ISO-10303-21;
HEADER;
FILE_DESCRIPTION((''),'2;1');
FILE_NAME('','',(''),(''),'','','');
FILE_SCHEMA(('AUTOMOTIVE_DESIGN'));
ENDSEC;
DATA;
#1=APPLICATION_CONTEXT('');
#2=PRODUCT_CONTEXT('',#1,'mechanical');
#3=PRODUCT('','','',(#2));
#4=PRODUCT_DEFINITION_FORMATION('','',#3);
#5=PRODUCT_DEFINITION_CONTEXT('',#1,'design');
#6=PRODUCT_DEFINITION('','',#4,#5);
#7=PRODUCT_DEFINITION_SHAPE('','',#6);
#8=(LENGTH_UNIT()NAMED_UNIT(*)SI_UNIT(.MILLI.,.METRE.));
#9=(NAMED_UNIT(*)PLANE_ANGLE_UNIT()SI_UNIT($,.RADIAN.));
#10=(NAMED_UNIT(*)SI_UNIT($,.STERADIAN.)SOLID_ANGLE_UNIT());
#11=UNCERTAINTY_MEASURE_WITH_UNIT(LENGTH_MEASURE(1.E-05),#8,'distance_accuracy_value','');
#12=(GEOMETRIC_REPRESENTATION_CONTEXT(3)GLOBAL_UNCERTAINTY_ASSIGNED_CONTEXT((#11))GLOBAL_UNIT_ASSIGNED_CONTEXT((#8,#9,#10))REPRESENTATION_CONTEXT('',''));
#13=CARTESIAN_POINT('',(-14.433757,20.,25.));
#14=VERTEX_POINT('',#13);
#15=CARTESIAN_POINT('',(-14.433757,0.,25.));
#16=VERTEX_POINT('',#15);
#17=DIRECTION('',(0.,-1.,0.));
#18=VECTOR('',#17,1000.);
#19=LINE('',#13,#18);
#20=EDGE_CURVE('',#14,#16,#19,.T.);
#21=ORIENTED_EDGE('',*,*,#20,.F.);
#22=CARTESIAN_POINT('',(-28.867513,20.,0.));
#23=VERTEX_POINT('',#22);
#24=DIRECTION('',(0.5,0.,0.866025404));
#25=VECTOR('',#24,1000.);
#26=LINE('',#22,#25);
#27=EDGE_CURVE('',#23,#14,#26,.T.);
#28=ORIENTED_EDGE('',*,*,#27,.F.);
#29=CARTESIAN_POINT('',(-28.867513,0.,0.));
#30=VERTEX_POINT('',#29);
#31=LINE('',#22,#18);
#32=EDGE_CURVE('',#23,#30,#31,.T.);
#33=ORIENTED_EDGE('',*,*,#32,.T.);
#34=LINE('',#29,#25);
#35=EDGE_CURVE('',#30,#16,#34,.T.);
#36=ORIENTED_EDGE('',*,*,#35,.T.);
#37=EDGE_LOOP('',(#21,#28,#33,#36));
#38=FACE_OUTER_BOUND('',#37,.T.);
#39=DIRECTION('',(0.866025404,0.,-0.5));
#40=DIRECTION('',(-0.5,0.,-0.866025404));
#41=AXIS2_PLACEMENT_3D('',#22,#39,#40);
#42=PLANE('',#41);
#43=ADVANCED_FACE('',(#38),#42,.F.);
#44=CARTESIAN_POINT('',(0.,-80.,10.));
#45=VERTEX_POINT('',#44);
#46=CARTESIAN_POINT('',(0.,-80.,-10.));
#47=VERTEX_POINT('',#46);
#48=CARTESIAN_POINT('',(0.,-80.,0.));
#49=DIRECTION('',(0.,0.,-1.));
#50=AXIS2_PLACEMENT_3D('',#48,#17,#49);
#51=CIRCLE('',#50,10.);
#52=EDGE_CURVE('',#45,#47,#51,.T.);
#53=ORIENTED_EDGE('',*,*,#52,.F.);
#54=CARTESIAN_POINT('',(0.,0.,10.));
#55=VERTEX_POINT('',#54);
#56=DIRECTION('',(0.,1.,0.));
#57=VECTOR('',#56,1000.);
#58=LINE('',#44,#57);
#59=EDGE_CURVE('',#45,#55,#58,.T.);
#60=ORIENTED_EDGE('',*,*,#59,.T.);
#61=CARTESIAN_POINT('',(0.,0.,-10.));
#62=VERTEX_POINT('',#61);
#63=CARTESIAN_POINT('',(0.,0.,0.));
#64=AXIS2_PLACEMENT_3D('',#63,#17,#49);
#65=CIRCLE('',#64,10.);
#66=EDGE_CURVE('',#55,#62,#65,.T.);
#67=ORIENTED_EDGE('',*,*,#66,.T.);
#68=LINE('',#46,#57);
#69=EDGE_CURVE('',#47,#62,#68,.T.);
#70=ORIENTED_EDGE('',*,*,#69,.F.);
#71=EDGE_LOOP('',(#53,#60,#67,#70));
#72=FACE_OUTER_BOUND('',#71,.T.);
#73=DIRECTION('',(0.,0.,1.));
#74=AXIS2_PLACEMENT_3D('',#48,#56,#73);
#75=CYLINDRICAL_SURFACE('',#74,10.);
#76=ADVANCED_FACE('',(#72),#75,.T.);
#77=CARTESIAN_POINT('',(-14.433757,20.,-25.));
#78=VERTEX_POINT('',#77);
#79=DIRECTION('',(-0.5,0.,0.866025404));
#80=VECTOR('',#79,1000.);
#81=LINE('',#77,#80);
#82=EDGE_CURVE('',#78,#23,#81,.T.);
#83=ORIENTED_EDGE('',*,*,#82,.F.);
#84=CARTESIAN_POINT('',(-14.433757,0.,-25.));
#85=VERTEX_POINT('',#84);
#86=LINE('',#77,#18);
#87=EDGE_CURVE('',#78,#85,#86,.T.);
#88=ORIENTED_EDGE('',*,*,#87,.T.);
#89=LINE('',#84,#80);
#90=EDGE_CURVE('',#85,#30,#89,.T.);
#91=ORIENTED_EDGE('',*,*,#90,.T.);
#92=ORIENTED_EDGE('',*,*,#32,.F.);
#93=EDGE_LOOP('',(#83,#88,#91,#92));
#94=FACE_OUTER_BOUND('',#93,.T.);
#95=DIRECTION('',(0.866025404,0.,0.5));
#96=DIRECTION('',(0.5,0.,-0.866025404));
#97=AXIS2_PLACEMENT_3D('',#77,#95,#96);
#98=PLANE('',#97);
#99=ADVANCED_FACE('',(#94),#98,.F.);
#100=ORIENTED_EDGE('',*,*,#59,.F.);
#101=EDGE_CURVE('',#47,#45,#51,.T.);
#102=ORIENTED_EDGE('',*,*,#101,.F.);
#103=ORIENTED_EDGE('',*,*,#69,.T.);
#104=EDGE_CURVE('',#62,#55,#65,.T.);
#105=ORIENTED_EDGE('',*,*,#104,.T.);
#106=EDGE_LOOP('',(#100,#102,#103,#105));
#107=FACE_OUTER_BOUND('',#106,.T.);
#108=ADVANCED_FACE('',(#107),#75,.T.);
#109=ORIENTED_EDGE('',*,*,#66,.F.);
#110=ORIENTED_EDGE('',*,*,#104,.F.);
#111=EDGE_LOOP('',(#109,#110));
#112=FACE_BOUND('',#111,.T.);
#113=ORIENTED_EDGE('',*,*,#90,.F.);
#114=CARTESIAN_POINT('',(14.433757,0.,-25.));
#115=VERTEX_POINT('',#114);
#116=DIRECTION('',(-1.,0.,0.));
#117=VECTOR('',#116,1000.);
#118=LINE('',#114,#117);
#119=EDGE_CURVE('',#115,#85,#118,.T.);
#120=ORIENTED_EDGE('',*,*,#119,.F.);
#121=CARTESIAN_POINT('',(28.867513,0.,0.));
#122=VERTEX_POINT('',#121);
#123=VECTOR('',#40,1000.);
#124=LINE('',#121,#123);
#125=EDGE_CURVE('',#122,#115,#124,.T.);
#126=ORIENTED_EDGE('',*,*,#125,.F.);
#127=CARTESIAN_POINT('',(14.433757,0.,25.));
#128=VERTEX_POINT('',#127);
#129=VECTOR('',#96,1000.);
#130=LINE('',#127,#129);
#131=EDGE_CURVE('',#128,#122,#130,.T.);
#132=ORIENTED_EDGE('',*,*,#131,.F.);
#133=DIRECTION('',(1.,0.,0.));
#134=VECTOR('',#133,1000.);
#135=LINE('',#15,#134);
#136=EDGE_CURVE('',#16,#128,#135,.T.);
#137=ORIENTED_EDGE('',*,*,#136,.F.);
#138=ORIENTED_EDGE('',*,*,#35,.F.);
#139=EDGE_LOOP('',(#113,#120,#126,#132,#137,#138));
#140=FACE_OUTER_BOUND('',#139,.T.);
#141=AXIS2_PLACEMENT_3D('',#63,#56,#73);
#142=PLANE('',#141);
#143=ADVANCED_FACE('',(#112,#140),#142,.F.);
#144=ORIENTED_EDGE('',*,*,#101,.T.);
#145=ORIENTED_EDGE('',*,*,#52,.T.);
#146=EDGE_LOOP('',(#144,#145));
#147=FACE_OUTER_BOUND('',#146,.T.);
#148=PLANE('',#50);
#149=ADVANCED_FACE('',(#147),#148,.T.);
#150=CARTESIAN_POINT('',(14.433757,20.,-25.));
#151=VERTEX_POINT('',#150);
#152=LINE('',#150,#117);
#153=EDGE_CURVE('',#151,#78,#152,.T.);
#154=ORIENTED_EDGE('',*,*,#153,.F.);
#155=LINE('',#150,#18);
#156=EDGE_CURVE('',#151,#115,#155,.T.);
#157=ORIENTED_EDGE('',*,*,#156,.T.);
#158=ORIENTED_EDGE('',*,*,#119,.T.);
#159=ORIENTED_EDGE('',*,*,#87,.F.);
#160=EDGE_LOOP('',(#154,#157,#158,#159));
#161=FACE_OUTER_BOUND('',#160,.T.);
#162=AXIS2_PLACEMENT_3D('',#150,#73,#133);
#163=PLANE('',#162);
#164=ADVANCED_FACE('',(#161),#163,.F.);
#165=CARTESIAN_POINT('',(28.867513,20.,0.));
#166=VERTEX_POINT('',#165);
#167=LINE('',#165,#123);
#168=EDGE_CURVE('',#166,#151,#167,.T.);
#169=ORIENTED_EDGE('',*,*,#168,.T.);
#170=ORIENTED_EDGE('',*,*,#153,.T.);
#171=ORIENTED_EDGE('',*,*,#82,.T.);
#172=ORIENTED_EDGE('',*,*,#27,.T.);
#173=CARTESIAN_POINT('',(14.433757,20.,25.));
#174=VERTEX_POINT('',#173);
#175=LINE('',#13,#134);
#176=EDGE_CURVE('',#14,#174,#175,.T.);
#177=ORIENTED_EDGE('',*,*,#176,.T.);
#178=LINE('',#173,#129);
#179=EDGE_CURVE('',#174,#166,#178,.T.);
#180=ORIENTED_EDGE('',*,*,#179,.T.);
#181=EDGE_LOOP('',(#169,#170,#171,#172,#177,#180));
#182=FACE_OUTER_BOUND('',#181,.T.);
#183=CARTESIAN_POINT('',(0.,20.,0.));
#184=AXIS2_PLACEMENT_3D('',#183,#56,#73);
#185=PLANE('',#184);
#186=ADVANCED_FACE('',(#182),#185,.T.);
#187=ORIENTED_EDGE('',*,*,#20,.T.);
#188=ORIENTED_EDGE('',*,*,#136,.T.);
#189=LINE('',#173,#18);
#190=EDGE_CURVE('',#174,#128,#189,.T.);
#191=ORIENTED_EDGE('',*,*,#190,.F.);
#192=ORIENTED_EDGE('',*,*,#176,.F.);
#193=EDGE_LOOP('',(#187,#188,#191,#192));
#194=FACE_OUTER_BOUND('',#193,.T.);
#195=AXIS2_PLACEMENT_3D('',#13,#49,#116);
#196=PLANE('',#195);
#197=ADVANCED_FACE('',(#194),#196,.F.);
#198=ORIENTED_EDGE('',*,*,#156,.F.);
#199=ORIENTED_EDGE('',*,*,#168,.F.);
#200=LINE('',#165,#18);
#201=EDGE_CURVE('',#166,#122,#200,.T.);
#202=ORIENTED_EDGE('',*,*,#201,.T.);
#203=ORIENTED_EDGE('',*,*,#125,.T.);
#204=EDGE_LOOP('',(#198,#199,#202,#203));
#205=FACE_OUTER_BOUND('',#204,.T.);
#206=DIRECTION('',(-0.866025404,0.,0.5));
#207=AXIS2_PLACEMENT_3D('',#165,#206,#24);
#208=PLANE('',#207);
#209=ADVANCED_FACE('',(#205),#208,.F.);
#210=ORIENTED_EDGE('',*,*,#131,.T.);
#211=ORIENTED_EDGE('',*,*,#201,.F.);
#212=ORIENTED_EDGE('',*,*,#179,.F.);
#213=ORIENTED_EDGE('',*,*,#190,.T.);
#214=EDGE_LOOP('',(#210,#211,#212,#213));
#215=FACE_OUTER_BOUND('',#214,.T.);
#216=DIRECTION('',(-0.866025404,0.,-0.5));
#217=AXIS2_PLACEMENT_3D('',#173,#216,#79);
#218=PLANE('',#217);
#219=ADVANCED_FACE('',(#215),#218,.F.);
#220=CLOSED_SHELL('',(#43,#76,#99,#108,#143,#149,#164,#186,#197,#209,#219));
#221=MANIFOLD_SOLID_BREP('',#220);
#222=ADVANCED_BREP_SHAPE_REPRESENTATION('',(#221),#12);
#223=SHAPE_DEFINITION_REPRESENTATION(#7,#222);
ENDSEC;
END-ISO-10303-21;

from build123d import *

# Parameters (mm, degrees)
HEX_HEAD_50AF_X20_DEPTH = 20
SHANK_SKETCH_20_R       = 10
SHANK_20X80_DEPTH       = 80


with BuildPart() as part:
    # Hex Head Sketch 50AF → Hex Head 50AF x20 (new body)
    with BuildSketch(Plane(origin=(0, 0, 0), x_dir=(1, 0, 0), z_dir=(0, 1, 0))):
        Polygon((28.867513459, 0), (14.43375673, 25), (-14.43375673, 25), (-28.867513459, 0), (-14.43375673, -25), (14.43375673, -25), align=None)
    extrude(amount=HEX_HEAD_50AF_X20_DEPTH)

    # Shank Sketch Ø20 → Shank Ø20x80 (add)
    with BuildSketch(Plane.XZ):
        with Locations(Location((0, 0, 0), (0, 0, 270))):
            Circle(SHANK_SKETCH_20_R)
    extrude(amount=SHANK_20X80_DEPTH)


solid = part.part
